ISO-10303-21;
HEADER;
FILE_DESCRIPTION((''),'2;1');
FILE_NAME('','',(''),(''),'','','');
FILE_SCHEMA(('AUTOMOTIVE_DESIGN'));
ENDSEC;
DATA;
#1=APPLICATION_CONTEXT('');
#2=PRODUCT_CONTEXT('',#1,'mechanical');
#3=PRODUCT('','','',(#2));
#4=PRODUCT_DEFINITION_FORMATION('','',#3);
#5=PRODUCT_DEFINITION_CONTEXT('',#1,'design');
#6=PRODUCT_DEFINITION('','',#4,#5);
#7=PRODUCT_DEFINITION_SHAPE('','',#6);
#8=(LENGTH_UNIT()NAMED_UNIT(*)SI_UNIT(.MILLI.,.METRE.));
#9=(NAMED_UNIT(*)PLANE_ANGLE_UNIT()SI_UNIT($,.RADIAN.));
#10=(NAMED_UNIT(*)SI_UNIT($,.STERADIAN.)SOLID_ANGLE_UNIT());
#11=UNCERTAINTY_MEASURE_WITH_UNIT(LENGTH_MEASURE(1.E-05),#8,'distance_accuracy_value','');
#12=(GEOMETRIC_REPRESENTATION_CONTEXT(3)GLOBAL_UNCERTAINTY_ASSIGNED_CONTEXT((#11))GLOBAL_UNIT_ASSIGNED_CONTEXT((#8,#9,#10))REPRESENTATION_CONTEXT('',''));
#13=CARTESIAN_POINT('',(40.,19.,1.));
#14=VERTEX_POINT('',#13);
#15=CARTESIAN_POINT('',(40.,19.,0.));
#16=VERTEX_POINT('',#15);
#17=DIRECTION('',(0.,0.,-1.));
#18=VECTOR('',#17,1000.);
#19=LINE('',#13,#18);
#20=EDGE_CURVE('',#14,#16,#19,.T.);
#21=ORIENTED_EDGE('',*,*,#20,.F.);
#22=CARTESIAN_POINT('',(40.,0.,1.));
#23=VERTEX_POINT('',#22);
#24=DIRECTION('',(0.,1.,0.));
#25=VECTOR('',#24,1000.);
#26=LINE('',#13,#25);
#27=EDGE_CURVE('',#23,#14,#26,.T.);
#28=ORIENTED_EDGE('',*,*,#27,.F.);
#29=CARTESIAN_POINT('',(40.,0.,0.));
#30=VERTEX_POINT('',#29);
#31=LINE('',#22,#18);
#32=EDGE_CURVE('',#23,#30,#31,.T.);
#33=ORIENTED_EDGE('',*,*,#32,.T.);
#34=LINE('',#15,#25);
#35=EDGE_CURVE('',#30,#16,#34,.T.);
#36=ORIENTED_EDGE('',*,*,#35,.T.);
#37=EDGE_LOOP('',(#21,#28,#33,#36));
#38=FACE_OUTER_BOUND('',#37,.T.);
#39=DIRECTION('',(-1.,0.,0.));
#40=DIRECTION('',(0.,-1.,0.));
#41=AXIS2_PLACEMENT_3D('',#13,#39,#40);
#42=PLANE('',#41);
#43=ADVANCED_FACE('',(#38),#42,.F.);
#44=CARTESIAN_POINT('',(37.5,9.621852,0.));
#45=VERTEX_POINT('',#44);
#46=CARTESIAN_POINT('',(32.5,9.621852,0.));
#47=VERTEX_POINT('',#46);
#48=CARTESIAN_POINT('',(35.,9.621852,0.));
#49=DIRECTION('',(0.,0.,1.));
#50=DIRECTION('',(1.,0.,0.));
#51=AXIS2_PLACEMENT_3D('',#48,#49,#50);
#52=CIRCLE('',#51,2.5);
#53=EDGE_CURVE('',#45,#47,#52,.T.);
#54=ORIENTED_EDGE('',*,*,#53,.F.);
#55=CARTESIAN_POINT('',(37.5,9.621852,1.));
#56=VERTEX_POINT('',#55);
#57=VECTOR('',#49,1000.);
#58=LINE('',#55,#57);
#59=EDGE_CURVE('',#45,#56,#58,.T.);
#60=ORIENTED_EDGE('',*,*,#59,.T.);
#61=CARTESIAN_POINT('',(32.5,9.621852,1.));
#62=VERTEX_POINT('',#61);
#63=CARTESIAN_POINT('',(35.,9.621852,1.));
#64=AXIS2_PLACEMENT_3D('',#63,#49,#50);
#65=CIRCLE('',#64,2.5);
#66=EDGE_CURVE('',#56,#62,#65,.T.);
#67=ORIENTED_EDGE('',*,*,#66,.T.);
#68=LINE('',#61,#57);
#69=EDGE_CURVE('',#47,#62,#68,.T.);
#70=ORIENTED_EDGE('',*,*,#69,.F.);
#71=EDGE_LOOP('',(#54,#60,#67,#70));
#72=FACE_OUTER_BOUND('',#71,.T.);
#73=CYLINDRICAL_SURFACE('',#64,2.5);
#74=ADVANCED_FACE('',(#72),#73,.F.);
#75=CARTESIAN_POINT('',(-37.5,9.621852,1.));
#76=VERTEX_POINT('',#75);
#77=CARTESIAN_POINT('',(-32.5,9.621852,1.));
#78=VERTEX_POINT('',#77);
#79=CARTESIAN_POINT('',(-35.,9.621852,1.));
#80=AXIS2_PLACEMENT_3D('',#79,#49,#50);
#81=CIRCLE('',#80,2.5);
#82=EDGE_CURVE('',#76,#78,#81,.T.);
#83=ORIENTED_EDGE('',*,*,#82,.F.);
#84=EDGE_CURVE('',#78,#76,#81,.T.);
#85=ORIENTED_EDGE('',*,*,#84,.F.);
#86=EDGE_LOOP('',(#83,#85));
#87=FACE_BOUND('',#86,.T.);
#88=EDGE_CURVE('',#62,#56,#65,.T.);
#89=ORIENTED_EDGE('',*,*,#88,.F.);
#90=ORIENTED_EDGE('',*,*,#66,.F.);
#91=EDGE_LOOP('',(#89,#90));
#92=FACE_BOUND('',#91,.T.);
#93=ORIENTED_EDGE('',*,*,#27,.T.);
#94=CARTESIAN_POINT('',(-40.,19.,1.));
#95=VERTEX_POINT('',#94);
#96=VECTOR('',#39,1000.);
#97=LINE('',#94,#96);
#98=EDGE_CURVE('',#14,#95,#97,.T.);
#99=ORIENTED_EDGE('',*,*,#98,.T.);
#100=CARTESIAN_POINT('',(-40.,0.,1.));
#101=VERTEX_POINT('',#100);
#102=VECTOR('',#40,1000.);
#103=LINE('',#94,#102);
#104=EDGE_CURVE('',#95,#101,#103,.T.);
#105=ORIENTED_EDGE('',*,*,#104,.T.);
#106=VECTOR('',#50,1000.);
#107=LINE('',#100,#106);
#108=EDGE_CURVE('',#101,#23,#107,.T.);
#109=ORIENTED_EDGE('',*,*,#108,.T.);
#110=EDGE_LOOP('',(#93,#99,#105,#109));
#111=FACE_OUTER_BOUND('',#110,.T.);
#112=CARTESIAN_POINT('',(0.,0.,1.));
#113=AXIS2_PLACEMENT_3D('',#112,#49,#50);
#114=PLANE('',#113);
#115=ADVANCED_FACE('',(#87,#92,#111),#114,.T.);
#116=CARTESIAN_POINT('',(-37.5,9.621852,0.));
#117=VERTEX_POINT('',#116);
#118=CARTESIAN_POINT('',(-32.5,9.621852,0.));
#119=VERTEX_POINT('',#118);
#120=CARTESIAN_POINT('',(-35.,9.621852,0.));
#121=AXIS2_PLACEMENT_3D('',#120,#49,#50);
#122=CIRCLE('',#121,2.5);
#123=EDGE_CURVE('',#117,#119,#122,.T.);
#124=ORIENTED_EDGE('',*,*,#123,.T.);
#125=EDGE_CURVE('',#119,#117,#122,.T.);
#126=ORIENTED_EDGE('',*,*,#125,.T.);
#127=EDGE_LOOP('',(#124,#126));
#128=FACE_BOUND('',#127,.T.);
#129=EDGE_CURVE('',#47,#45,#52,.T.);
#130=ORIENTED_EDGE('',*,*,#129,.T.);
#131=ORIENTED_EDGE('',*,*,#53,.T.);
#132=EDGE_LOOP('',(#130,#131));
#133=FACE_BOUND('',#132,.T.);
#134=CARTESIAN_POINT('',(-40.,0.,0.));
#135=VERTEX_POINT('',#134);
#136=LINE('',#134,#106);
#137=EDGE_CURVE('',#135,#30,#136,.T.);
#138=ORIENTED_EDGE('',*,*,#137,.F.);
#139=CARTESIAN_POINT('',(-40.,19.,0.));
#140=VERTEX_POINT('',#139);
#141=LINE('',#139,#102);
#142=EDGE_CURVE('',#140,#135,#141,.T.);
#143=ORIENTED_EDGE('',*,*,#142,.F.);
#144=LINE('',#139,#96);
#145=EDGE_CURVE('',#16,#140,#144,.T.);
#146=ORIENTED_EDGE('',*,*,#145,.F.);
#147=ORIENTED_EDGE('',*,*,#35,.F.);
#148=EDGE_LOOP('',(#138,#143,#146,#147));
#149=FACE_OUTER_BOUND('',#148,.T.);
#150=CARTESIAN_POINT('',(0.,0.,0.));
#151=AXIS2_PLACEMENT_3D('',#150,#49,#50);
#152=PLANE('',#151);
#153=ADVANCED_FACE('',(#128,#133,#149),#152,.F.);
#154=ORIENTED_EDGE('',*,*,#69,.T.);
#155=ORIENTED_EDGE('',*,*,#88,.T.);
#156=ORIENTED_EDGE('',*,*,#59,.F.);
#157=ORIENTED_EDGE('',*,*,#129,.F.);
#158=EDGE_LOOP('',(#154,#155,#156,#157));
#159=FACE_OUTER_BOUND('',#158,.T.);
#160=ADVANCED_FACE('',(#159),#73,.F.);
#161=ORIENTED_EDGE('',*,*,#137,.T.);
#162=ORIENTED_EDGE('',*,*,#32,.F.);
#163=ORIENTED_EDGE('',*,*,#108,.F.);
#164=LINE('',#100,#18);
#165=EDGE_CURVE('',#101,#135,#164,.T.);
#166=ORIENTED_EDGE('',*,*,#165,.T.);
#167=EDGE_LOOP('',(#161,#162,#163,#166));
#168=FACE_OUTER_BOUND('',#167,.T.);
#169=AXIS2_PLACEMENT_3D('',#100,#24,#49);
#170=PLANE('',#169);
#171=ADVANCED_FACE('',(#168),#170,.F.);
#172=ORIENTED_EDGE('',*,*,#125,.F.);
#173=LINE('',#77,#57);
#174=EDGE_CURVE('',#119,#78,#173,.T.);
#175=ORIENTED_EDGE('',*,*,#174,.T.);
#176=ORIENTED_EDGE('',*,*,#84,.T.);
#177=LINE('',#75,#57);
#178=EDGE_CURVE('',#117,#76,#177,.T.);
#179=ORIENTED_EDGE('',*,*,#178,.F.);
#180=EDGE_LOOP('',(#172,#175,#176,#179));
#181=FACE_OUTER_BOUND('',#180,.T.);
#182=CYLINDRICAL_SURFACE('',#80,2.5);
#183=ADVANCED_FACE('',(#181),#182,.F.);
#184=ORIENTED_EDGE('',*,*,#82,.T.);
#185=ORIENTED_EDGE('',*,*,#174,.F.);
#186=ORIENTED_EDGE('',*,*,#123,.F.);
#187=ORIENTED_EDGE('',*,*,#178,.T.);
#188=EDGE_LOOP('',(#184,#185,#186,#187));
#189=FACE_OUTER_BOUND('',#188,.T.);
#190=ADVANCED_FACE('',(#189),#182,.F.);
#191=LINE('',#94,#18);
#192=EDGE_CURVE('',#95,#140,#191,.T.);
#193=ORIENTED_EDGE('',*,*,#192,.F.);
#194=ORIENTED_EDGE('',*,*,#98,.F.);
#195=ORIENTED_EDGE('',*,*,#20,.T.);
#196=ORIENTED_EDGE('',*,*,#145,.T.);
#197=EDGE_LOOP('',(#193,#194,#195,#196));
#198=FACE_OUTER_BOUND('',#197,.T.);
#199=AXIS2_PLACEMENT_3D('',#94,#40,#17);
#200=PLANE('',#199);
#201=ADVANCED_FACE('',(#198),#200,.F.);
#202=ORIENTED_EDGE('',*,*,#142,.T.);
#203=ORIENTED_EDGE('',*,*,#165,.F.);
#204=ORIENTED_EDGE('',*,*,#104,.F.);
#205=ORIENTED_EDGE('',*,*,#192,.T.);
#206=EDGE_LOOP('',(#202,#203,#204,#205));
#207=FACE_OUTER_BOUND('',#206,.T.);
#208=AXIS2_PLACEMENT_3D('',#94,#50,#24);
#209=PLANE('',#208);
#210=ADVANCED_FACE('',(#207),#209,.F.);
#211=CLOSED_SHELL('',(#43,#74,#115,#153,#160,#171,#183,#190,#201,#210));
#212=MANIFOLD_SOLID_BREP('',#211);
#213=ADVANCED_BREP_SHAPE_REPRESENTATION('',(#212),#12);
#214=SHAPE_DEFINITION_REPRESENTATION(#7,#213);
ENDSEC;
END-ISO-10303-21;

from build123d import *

# Parameters (mm, degrees)
SKETCH_1_W            = 80
SKETCH_1_H            = 19
EXTRUDE_1_DEPTH       = 1
HOLE_WIZARD_5_0_5_1_D = 5


with BuildPart() as part:
    # 草图1 → 凸台-拉伸1 (new body)
    with BuildSketch(Plane.XY):
        with Locations((0, 9.5)):
            Rectangle(SKETCH_1_W, SKETCH_1_H)
    extrude(amount=EXTRUDE_1_DEPTH)

    # Ø5.0 (5) 直径孔1 (through all)
    with Locations(Plane.XY.offset(1)):
        with Locations((-35, 9.621851999), (35, 9.621851999)):
            Hole(HOLE_WIZARD_5_0_5_1_D / 2)


solid = part.part
